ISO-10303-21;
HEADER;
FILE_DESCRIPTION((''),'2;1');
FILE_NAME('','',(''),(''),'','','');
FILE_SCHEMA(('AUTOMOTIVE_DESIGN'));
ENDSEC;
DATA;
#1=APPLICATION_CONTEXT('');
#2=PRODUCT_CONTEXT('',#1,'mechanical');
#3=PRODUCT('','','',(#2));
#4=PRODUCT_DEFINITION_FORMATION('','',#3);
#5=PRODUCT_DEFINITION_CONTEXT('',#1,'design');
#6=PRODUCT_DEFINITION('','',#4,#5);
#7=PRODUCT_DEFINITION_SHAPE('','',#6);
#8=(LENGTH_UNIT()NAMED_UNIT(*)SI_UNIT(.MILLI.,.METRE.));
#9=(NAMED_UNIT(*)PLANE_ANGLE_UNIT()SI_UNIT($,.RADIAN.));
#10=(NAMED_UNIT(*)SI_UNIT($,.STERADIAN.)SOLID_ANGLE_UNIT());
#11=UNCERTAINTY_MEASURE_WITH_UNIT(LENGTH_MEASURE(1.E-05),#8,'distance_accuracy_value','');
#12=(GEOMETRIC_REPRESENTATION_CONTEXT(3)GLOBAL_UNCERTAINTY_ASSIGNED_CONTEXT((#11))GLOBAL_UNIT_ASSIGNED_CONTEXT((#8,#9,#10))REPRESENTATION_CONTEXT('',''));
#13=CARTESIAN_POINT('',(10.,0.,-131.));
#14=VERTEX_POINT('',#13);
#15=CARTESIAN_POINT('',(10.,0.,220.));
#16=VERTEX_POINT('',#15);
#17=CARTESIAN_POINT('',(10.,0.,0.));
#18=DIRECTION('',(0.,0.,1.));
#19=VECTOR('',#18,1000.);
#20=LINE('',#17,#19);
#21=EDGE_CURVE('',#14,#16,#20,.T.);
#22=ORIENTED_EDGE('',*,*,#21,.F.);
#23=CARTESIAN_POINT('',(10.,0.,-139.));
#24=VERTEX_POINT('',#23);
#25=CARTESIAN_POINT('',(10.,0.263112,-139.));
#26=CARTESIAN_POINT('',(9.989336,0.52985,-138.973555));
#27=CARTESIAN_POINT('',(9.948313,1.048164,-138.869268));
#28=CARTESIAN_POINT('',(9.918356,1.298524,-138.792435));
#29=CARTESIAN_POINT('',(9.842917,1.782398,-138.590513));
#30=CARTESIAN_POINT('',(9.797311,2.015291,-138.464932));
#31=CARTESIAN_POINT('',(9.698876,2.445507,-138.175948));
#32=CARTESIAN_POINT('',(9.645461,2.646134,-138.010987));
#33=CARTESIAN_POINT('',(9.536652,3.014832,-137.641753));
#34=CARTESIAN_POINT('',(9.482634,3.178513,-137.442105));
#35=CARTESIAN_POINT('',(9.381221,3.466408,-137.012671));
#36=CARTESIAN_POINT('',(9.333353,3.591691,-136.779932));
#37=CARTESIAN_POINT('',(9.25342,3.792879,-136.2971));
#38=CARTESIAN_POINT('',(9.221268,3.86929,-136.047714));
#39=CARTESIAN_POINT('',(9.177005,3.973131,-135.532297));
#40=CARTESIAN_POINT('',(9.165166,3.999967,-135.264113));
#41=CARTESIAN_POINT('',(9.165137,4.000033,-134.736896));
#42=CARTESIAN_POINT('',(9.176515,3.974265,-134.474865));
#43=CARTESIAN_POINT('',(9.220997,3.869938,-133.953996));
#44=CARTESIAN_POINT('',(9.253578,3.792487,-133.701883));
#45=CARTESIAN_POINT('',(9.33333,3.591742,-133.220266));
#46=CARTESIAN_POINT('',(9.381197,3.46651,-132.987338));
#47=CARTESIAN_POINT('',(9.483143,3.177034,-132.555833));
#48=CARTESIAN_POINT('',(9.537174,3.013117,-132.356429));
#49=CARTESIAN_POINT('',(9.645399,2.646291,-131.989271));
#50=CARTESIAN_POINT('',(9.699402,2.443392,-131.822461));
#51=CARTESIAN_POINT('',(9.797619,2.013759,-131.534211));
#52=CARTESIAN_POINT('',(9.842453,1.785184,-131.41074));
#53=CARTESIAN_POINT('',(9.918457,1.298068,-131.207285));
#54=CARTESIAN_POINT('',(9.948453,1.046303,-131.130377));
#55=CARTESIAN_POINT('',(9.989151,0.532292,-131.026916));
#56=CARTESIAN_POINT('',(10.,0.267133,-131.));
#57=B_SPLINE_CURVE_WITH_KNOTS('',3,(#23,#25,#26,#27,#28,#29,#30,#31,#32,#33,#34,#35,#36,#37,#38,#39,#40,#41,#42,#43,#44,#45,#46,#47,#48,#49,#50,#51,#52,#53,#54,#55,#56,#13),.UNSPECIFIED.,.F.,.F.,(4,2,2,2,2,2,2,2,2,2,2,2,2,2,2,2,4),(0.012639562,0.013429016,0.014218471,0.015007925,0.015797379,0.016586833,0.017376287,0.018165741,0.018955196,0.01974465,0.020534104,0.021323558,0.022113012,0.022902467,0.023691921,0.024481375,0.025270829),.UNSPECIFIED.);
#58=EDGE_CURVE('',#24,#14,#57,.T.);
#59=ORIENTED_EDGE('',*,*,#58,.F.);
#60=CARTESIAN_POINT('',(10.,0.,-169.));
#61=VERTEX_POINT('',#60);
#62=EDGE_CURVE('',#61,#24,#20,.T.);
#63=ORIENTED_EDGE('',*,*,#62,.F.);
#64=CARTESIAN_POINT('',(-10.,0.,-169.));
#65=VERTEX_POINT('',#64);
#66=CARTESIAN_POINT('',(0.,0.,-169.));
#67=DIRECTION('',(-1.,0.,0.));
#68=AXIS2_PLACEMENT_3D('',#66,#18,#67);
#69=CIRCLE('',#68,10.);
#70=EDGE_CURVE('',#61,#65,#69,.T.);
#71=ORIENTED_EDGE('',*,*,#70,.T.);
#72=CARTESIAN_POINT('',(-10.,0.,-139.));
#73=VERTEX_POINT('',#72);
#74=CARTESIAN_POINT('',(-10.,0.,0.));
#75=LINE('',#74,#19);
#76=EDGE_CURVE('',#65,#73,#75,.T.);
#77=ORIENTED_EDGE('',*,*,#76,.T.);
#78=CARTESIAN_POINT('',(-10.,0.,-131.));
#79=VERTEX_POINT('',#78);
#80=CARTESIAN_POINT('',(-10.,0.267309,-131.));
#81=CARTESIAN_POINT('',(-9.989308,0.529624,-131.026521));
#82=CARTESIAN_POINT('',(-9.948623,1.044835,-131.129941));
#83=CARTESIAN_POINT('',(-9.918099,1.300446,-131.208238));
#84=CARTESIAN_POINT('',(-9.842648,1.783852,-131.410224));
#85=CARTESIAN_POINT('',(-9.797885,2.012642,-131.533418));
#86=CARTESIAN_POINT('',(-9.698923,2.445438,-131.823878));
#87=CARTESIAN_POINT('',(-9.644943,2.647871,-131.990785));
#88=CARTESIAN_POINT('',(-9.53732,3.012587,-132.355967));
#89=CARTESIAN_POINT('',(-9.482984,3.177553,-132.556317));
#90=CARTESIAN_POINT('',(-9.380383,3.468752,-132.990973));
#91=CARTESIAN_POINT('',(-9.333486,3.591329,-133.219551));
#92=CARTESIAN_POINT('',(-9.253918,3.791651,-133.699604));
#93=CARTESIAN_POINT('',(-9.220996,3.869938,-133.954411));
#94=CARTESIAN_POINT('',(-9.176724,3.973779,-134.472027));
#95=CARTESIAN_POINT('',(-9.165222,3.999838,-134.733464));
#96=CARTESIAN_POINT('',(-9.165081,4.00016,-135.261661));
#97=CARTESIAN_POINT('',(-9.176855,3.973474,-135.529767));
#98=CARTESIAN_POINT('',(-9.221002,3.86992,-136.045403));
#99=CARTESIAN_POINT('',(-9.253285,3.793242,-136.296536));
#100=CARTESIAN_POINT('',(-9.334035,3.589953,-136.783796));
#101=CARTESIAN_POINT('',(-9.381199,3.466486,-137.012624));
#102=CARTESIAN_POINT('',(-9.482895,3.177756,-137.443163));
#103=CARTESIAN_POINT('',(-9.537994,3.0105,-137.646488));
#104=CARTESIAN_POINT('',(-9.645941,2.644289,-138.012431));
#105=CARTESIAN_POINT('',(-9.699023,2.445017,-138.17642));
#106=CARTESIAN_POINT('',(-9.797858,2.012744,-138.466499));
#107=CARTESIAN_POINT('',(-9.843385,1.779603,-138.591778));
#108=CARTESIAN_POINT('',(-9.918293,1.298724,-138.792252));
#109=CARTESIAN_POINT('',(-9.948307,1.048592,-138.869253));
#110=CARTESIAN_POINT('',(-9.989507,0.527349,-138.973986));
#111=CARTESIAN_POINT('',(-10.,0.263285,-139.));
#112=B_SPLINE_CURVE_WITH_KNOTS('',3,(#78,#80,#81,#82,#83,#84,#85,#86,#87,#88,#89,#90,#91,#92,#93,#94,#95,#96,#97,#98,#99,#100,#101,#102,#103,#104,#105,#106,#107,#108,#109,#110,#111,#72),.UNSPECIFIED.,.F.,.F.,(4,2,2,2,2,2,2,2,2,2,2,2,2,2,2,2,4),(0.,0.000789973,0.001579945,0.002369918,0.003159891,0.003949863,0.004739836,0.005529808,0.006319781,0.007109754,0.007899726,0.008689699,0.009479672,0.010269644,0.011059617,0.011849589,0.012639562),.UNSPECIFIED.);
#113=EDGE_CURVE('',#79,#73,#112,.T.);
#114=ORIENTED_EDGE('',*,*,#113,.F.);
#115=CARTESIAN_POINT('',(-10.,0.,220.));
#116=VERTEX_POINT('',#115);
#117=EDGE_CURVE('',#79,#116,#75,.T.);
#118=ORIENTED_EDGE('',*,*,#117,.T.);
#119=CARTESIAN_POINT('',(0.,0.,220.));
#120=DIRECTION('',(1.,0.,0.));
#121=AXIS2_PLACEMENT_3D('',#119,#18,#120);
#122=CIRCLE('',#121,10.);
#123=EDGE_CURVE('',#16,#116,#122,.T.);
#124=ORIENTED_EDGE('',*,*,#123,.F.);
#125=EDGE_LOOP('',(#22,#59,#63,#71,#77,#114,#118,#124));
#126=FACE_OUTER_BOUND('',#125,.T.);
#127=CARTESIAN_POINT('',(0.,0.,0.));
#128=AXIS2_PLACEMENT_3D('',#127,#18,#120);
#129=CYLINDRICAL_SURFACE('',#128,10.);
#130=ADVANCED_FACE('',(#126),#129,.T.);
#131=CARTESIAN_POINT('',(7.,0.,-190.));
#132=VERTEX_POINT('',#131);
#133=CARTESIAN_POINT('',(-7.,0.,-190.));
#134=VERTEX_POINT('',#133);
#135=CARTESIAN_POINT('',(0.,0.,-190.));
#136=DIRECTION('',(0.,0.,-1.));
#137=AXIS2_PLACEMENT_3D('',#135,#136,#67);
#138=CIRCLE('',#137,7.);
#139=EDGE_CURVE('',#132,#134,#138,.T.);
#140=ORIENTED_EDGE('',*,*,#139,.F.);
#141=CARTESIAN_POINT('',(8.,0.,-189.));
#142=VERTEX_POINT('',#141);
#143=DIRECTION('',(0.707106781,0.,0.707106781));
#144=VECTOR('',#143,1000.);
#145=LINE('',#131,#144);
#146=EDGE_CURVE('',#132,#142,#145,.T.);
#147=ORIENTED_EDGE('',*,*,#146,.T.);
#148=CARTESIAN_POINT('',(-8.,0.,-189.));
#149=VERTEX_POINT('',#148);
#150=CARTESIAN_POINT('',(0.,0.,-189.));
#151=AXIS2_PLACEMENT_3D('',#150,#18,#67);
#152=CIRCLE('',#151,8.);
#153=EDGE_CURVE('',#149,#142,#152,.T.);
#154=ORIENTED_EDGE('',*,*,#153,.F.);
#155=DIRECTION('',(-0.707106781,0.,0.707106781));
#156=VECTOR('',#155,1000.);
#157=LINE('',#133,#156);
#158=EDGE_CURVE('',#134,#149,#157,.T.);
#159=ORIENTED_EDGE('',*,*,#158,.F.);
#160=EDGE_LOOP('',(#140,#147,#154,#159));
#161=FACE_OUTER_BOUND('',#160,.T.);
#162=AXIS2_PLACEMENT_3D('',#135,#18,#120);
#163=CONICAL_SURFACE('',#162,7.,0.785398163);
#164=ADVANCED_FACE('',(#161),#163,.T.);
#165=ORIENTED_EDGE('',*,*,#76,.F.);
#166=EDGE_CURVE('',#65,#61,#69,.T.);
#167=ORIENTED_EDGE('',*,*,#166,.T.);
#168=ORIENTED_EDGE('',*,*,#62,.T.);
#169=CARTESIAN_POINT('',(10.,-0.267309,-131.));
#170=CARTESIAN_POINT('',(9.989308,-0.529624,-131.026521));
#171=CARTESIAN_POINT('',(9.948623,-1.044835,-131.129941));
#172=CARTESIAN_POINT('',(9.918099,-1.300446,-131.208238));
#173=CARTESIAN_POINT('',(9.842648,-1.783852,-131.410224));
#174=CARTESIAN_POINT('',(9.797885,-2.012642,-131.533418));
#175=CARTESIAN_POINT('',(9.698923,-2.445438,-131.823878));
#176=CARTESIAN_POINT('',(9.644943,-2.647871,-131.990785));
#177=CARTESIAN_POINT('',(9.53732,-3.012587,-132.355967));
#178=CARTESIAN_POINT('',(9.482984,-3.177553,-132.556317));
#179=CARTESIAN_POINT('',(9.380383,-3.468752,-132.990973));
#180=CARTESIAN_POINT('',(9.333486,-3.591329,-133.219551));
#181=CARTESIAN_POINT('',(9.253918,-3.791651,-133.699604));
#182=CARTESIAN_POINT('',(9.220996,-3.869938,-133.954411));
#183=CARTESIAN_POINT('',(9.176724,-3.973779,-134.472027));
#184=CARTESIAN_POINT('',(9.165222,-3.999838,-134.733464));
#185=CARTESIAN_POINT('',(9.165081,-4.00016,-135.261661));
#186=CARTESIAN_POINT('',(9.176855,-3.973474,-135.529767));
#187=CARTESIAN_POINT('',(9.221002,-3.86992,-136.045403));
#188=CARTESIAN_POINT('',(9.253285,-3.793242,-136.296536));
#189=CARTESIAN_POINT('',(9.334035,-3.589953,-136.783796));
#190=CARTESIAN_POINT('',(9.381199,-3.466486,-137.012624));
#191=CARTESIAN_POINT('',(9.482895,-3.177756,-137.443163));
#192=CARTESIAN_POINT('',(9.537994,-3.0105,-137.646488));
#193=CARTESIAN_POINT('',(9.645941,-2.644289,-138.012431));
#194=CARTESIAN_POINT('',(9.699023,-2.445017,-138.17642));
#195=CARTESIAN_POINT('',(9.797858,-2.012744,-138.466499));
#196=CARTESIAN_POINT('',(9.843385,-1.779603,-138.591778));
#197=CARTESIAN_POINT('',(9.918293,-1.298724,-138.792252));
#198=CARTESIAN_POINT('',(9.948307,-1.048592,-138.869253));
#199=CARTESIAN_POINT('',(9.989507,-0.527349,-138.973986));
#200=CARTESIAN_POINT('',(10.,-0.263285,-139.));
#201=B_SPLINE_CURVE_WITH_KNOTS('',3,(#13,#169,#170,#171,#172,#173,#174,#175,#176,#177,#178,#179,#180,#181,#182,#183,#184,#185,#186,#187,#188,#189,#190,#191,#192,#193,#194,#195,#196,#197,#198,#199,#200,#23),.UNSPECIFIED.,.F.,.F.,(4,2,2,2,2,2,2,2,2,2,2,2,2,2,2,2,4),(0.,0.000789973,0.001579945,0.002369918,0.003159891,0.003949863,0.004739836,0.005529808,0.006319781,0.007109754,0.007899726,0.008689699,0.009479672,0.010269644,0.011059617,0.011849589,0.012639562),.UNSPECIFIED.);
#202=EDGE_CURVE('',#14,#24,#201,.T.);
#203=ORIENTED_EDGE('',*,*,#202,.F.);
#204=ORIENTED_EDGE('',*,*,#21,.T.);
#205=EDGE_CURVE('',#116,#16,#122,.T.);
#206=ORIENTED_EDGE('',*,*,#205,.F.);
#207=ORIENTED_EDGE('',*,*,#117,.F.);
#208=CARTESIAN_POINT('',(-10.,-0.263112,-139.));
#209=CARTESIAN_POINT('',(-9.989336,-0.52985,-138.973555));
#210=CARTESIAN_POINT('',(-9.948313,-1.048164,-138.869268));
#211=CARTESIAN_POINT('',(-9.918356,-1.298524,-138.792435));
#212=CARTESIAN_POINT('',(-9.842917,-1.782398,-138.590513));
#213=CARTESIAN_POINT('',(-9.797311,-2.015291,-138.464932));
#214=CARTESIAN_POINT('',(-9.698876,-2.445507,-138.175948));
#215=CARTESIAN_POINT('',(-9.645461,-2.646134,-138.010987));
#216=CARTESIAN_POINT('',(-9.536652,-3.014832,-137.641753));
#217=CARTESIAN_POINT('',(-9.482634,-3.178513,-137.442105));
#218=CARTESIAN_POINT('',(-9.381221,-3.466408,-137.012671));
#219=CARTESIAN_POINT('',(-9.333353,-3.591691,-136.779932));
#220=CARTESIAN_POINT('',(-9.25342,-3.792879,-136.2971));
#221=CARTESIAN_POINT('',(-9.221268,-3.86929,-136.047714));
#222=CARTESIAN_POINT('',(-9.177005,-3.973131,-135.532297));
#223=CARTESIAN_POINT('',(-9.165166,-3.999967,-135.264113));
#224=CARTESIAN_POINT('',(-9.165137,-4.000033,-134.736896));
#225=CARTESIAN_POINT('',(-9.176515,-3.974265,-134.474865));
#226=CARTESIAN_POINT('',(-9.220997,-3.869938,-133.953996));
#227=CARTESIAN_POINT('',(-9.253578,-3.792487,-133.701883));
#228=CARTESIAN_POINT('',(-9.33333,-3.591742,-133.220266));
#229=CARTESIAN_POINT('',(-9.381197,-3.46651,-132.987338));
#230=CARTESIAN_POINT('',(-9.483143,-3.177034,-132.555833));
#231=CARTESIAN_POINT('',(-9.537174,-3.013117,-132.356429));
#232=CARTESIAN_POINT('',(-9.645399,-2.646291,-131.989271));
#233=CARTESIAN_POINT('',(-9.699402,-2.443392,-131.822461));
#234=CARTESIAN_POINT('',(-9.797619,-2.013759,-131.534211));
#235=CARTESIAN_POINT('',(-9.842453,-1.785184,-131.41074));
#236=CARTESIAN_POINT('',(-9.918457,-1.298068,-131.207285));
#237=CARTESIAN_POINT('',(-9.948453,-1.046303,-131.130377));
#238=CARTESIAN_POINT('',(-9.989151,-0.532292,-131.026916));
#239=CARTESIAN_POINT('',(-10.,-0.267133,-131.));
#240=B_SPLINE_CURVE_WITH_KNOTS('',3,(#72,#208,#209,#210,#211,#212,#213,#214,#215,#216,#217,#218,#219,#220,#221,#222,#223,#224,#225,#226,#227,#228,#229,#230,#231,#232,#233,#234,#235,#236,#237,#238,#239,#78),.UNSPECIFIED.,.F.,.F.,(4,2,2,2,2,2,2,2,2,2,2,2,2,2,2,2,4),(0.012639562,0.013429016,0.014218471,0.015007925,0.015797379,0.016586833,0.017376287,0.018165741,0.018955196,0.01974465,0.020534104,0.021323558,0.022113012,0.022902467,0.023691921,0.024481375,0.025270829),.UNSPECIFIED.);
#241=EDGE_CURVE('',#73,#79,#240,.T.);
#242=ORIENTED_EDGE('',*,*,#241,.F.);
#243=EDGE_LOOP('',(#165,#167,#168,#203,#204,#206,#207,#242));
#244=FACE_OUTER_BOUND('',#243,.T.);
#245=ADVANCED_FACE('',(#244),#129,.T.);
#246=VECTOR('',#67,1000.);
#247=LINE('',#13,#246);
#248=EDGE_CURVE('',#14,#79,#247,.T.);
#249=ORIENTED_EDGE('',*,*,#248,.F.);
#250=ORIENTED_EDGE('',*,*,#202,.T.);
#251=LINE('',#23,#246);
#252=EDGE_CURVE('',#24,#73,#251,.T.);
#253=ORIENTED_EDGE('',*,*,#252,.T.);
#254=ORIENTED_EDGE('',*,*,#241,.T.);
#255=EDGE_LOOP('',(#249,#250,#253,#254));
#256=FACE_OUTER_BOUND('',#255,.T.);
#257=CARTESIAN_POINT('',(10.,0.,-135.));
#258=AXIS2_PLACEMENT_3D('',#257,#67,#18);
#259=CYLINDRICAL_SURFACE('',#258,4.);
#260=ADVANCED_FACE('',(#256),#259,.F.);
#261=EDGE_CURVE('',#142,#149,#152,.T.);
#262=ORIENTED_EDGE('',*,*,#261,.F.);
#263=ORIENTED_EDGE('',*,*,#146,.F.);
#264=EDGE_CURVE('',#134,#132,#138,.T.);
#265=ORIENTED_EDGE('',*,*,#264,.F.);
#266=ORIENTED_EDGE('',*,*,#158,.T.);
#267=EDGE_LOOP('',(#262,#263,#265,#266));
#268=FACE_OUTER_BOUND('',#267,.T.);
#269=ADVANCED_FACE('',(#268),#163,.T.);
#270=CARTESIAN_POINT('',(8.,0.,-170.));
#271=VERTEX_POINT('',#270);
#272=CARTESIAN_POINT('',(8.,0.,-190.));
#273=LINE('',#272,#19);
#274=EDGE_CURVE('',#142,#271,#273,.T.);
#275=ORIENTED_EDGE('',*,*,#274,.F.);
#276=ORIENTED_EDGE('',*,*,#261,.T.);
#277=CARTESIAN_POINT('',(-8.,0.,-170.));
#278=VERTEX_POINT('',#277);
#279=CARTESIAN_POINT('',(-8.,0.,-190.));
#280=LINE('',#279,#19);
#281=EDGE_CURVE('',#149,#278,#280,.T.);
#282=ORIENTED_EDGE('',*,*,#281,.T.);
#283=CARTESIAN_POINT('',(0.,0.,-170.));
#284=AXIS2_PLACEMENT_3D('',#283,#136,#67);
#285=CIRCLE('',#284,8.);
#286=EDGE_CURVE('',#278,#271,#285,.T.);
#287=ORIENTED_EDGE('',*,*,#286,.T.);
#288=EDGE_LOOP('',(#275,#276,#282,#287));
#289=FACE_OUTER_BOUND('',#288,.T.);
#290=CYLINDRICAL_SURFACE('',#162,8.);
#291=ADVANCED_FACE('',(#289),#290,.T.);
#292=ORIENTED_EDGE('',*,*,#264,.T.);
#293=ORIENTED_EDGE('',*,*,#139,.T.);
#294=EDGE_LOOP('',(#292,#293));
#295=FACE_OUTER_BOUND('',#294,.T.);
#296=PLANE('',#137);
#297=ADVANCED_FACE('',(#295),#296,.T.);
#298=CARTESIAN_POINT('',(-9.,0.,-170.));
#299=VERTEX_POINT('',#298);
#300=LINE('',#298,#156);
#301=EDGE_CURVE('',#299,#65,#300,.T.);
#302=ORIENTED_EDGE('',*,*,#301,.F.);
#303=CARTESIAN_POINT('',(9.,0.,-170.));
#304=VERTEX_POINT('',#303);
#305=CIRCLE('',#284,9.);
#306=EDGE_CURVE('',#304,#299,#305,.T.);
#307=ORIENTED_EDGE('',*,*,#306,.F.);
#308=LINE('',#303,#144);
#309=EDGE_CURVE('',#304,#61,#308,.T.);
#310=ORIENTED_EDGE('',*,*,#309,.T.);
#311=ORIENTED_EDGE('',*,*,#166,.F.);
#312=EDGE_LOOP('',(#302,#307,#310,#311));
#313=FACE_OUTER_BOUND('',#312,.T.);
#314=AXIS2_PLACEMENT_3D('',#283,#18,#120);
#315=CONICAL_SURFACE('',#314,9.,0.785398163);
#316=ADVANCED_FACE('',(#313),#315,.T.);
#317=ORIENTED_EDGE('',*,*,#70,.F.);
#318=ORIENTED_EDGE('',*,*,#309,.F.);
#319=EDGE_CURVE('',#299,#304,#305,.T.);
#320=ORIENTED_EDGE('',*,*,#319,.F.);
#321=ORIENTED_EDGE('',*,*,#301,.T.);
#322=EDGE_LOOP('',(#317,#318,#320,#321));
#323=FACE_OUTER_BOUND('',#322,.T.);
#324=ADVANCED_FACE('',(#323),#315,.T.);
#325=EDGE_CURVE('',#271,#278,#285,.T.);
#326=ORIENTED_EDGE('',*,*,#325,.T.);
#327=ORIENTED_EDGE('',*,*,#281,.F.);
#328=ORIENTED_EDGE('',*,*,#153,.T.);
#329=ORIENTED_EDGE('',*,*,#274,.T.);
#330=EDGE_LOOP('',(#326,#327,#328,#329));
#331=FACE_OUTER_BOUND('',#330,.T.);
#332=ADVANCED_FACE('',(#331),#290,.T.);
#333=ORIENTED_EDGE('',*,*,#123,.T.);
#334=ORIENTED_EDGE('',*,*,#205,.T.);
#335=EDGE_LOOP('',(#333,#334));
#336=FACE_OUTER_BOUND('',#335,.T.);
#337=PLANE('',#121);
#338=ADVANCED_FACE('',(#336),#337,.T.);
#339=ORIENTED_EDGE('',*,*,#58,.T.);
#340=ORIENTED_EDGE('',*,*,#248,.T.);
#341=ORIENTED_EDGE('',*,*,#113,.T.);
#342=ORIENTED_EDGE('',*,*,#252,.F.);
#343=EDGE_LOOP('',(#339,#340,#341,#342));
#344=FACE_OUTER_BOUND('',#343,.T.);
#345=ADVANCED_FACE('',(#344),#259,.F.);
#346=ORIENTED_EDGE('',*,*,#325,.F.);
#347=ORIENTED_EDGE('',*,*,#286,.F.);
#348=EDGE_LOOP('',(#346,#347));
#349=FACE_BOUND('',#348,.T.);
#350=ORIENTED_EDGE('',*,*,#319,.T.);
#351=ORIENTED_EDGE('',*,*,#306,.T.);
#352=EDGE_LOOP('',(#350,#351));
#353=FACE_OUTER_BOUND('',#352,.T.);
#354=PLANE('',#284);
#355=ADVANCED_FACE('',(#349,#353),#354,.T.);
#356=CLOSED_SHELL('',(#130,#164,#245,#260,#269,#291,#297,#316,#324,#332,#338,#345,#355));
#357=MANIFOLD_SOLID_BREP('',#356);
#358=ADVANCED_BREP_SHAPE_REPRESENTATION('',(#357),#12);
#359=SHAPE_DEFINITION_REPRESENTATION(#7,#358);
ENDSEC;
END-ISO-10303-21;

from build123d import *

# Parameters (mm, degrees)
SKETCH2_W               = 150
SKETCH2_H               = 10
CUT_EXTRUDE1_DEPTH      = 10
CUT_EXTRUDE1_DEPTH_BACK = 10
SKETCH5_R               = 4
SKETCH6_R               = 10
BOSS_EXTRUDE1_DEPTH     = 20
SKETCH7_R               = 8
BOSS_EXTRUDE2_DEPTH     = 20
CHAMFER1_SIZE           = 1
BOSS_EXTRUDE4_START     = 220
SKETCH8_R               = 10
BOSS_EXTRUDE4_DEPTH     = 220


with BuildPart() as part:
    # Sketch2 → Revolve4 (revolve)
    with BuildSketch(Plane(origin=(0, 0, 0), x_dir=(0, 0, -1), z_dir=(1, 0, 0)), mode=Mode.PRIVATE) as revolve4_sk:
        with Locations((75, 5)):
            Rectangle(SKETCH2_W, SKETCH2_H)
    revolve(revolve4_sk.sketch.rotate(Axis((0, 0, 0), (0, 0, -1)), 90), axis=Axis((0, 0, 0), (0, 0, -1)))

    # Sketch5 → Cut-Extrude1 (cut, two sides: drawn at the far end of the back side and taken through both)
    with BuildSketch(Plane(origin=(0, 0, 0), x_dir=(0, 0, -1), z_dir=(1, 0, 0)).offset(-CUT_EXTRUDE1_DEPTH_BACK)):
        with Locations(Location((135, 0, 0), (0, 0, 180))):
            Circle(SKETCH5_R)
    extrude(amount=CUT_EXTRUDE1_DEPTH + CUT_EXTRUDE1_DEPTH_BACK, mode=Mode.SUBTRACT)

    # Sketch6 → Boss-Extrude1 (add)
    with BuildSketch(Plane(origin=(0, 0, -150), x_dir=(-1, 0, 0), z_dir=(0, 0, -1))):
        with Locations(Location((0, 0, 0), (0, 0, 180))):
            Circle(SKETCH6_R)
    extrude(amount=BOSS_EXTRUDE1_DEPTH)

    # Sketch7 → Boss-Extrude2 (add)
    with BuildSketch(Plane(origin=(0, 0, -170), x_dir=(-1, 0, 0), z_dir=(0, 0, -1))):
        Circle(SKETCH7_R)
    extrude(amount=BOSS_EXTRUDE2_DEPTH)

    # Chamfer1
    chamfer1_edges = [part.edges().sort_by_distance(p)[0] for p in [
        (-10, 0, -170),
        (8, 0, -190),
    ]]
    chamfer(chamfer1_edges, length=CHAMFER1_SIZE)

    # Sketch8 → Boss-Extrude4 (add)
    with BuildSketch(Plane.XY.offset(BOSS_EXTRUDE4_START)):
        Circle(SKETCH8_R)
    extrude(amount=-BOSS_EXTRUDE4_DEPTH)


solid = part.part
